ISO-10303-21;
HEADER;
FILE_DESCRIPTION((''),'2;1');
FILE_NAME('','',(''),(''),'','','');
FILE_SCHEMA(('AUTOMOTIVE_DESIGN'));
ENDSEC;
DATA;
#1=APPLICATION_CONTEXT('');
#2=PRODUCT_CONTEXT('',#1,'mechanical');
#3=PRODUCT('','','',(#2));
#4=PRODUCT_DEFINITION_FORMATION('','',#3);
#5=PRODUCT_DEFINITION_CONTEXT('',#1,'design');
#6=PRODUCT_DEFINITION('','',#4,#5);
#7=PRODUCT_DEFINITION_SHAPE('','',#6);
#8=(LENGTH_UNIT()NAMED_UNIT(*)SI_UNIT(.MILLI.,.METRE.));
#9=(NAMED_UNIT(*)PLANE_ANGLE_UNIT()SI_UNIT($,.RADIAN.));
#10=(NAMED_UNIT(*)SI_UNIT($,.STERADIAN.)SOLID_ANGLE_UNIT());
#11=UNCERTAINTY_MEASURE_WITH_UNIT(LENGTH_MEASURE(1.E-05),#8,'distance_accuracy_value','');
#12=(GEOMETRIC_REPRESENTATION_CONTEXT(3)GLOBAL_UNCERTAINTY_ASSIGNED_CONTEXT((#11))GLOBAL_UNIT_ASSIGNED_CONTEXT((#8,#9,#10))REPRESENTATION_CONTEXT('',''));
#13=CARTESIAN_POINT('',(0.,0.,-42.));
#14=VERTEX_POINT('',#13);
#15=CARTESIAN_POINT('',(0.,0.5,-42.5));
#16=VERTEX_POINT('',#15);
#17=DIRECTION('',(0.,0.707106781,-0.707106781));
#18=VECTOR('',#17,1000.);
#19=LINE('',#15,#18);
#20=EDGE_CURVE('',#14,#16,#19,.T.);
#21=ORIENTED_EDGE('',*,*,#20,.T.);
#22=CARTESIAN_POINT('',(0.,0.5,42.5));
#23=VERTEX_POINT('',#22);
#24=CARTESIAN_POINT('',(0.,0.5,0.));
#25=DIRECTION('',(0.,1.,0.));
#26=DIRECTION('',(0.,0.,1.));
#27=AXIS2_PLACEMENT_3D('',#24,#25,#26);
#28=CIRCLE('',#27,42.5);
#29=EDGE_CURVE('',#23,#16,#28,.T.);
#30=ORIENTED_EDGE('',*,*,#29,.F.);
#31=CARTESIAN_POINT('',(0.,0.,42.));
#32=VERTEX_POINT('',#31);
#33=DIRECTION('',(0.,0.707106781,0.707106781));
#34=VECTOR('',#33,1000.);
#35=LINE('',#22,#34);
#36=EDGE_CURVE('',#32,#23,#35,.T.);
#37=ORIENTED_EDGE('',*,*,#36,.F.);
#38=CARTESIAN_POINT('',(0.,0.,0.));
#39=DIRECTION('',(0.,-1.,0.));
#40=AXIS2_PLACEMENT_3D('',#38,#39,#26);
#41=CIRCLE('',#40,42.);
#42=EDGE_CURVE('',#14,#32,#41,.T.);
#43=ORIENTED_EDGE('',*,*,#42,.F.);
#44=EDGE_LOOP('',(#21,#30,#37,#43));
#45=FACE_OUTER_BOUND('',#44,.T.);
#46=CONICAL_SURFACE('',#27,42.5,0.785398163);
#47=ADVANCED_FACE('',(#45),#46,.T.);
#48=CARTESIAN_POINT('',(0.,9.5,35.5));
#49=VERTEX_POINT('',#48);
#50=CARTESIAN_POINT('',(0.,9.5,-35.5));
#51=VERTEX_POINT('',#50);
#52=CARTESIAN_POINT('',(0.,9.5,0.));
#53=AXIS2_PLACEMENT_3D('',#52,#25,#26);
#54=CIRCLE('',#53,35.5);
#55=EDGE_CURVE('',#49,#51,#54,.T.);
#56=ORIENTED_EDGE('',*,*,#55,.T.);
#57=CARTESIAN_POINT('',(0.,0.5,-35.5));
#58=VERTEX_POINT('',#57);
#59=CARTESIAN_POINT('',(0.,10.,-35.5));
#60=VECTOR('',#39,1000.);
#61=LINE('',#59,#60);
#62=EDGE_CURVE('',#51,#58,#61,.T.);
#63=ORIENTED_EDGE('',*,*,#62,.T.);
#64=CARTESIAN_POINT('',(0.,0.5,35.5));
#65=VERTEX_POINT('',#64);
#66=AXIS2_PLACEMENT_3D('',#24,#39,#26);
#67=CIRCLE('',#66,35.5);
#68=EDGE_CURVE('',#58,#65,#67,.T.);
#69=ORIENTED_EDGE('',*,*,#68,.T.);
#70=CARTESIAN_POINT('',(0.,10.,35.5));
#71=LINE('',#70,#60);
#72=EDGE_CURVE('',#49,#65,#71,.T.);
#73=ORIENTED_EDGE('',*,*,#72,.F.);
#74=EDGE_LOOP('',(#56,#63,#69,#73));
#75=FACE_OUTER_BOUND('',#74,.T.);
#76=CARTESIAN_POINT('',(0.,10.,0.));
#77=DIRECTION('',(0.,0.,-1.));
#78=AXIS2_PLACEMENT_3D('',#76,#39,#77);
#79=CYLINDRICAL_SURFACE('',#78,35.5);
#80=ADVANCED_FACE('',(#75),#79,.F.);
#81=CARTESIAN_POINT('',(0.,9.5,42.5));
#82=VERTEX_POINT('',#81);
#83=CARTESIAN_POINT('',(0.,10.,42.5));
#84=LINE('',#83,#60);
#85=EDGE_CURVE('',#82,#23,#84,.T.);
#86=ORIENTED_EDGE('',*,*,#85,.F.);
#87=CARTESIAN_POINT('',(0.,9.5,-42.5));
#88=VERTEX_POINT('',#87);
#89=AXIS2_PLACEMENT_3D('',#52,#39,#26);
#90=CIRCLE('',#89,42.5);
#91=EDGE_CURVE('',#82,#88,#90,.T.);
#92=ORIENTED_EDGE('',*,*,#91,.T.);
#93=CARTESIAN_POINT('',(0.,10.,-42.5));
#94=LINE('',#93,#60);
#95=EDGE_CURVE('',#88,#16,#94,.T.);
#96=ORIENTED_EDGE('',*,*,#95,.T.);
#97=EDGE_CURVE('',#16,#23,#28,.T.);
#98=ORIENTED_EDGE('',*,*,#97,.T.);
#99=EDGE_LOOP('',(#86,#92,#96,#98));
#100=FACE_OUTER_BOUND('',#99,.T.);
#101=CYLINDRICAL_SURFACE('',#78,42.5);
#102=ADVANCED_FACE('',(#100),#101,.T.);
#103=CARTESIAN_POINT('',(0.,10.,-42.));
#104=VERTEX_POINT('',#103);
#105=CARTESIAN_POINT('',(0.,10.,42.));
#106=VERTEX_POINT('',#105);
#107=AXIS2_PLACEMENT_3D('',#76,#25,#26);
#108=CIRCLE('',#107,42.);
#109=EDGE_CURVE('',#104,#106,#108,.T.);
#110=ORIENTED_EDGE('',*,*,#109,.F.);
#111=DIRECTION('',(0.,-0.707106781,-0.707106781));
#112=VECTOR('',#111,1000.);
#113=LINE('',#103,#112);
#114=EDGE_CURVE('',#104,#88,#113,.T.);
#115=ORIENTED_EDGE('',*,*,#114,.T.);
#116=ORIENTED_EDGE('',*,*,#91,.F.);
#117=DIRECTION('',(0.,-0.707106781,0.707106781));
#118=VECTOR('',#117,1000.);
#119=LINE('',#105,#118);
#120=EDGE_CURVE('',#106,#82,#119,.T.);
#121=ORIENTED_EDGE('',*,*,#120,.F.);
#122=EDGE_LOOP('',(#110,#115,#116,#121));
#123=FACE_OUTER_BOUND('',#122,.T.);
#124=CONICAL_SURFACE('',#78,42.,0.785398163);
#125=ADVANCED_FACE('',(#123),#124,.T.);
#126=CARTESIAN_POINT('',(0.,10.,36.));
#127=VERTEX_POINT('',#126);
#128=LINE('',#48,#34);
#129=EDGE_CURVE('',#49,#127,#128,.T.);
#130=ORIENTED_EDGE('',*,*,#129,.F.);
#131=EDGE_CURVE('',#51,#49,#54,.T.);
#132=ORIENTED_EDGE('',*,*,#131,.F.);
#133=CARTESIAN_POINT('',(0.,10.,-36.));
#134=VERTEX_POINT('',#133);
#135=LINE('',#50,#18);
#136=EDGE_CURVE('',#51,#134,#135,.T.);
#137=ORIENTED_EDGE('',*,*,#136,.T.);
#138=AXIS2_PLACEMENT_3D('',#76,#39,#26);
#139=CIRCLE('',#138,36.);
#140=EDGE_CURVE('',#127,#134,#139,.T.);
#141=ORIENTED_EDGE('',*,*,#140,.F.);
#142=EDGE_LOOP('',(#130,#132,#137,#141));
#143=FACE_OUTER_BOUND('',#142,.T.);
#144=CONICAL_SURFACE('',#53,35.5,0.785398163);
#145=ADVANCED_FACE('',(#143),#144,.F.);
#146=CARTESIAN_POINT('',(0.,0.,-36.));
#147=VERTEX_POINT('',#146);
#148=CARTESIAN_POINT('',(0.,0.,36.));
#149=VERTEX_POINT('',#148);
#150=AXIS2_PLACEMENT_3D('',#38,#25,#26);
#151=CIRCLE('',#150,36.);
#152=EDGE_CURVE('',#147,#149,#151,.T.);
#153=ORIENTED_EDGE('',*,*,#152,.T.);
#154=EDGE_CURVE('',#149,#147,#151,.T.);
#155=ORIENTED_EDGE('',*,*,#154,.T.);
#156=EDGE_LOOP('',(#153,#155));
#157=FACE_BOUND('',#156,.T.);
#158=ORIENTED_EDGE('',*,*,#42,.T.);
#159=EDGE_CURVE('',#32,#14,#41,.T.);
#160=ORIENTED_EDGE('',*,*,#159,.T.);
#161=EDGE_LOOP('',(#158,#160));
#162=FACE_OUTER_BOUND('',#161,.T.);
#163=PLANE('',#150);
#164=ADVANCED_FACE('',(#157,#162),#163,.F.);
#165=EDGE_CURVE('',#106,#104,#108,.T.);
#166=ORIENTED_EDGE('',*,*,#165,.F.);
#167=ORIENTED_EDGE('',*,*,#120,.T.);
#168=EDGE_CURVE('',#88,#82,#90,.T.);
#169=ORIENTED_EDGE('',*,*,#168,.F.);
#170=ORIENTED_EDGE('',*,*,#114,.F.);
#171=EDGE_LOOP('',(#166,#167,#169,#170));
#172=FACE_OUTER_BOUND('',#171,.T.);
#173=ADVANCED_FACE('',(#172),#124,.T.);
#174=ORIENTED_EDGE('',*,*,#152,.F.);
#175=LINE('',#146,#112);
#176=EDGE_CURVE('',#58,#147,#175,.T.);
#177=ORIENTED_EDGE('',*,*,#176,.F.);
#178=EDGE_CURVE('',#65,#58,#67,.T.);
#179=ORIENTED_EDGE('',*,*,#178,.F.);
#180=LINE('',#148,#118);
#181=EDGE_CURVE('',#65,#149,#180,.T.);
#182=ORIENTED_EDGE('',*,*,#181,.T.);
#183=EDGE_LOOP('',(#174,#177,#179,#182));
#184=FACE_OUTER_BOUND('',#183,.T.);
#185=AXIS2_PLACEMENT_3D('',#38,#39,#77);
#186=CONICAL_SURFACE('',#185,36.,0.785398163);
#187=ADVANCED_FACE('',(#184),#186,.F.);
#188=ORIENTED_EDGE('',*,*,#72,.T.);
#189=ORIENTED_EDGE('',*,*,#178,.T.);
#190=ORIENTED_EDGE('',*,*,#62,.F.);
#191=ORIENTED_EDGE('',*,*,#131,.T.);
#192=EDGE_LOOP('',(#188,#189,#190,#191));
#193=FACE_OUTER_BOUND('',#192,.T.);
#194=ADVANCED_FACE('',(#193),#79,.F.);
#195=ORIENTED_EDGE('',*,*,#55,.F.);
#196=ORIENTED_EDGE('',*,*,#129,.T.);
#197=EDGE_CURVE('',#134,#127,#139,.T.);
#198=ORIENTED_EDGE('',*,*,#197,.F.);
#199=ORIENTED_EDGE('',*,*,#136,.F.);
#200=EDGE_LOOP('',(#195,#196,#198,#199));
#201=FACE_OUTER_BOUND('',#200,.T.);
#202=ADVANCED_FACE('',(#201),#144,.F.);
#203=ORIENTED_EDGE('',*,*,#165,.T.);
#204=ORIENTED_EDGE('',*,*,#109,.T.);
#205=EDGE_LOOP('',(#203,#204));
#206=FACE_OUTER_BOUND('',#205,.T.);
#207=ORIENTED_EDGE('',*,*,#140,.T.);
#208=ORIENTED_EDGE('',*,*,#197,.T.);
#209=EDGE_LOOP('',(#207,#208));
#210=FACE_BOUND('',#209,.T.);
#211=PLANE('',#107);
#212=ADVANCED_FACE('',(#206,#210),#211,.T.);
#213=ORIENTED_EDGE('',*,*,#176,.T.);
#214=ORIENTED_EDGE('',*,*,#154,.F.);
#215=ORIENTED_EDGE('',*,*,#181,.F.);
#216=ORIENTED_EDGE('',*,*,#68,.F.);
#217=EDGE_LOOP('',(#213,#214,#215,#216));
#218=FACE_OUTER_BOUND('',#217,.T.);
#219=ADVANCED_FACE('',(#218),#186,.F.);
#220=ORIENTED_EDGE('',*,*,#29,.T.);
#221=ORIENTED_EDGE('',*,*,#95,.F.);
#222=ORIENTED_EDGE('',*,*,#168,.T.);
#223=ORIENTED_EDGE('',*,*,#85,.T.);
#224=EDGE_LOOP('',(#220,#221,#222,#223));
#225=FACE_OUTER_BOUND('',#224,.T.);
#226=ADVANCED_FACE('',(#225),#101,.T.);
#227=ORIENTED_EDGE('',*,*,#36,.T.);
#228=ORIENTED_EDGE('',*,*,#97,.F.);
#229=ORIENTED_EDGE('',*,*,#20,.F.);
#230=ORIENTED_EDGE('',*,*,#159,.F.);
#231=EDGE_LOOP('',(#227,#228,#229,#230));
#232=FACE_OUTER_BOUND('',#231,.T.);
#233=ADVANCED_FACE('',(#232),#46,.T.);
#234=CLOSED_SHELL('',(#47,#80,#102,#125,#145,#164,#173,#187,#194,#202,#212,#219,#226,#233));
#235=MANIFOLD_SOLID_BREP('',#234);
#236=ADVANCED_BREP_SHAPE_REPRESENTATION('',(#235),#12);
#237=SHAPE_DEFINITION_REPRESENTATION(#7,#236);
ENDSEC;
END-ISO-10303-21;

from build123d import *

# Parameters (mm, degrees)
SKETCH1_R           = 42.5
SKETCH1_R_2         = 35.5
BOSS_EXTRUDE1_DEPTH = 10
CHAMFER2_SIZE       = 0.5


with BuildPart() as part:
    # Sketch1 → Boss-Extrude1 (new body)
    with BuildSketch(Plane(origin=(0, 0, 0), x_dir=(1, 0, 0), z_dir=(0, 1, 0))):
        with Locations(Location((0, 0, 0), (0, 0, 270))):
            Circle(SKETCH1_R)
        with Locations(Location((0, 0, 0), (0, 0, 270))):
            Circle(SKETCH1_R_2, mode=Mode.SUBTRACT)
    extrude(amount=BOSS_EXTRUDE1_DEPTH)

    # Chamfer2
    chamfer2_edges = [part.edges().sort_by_distance(p)[0] for p in [
        (0, 0, -42.5),
        (0, 10, -42.5),
        (0, 0, -35.5),
        (0, 10, -35.5),
    ]]
    chamfer(chamfer2_edges, length=CHAMFER2_SIZE)


solid = part.part
